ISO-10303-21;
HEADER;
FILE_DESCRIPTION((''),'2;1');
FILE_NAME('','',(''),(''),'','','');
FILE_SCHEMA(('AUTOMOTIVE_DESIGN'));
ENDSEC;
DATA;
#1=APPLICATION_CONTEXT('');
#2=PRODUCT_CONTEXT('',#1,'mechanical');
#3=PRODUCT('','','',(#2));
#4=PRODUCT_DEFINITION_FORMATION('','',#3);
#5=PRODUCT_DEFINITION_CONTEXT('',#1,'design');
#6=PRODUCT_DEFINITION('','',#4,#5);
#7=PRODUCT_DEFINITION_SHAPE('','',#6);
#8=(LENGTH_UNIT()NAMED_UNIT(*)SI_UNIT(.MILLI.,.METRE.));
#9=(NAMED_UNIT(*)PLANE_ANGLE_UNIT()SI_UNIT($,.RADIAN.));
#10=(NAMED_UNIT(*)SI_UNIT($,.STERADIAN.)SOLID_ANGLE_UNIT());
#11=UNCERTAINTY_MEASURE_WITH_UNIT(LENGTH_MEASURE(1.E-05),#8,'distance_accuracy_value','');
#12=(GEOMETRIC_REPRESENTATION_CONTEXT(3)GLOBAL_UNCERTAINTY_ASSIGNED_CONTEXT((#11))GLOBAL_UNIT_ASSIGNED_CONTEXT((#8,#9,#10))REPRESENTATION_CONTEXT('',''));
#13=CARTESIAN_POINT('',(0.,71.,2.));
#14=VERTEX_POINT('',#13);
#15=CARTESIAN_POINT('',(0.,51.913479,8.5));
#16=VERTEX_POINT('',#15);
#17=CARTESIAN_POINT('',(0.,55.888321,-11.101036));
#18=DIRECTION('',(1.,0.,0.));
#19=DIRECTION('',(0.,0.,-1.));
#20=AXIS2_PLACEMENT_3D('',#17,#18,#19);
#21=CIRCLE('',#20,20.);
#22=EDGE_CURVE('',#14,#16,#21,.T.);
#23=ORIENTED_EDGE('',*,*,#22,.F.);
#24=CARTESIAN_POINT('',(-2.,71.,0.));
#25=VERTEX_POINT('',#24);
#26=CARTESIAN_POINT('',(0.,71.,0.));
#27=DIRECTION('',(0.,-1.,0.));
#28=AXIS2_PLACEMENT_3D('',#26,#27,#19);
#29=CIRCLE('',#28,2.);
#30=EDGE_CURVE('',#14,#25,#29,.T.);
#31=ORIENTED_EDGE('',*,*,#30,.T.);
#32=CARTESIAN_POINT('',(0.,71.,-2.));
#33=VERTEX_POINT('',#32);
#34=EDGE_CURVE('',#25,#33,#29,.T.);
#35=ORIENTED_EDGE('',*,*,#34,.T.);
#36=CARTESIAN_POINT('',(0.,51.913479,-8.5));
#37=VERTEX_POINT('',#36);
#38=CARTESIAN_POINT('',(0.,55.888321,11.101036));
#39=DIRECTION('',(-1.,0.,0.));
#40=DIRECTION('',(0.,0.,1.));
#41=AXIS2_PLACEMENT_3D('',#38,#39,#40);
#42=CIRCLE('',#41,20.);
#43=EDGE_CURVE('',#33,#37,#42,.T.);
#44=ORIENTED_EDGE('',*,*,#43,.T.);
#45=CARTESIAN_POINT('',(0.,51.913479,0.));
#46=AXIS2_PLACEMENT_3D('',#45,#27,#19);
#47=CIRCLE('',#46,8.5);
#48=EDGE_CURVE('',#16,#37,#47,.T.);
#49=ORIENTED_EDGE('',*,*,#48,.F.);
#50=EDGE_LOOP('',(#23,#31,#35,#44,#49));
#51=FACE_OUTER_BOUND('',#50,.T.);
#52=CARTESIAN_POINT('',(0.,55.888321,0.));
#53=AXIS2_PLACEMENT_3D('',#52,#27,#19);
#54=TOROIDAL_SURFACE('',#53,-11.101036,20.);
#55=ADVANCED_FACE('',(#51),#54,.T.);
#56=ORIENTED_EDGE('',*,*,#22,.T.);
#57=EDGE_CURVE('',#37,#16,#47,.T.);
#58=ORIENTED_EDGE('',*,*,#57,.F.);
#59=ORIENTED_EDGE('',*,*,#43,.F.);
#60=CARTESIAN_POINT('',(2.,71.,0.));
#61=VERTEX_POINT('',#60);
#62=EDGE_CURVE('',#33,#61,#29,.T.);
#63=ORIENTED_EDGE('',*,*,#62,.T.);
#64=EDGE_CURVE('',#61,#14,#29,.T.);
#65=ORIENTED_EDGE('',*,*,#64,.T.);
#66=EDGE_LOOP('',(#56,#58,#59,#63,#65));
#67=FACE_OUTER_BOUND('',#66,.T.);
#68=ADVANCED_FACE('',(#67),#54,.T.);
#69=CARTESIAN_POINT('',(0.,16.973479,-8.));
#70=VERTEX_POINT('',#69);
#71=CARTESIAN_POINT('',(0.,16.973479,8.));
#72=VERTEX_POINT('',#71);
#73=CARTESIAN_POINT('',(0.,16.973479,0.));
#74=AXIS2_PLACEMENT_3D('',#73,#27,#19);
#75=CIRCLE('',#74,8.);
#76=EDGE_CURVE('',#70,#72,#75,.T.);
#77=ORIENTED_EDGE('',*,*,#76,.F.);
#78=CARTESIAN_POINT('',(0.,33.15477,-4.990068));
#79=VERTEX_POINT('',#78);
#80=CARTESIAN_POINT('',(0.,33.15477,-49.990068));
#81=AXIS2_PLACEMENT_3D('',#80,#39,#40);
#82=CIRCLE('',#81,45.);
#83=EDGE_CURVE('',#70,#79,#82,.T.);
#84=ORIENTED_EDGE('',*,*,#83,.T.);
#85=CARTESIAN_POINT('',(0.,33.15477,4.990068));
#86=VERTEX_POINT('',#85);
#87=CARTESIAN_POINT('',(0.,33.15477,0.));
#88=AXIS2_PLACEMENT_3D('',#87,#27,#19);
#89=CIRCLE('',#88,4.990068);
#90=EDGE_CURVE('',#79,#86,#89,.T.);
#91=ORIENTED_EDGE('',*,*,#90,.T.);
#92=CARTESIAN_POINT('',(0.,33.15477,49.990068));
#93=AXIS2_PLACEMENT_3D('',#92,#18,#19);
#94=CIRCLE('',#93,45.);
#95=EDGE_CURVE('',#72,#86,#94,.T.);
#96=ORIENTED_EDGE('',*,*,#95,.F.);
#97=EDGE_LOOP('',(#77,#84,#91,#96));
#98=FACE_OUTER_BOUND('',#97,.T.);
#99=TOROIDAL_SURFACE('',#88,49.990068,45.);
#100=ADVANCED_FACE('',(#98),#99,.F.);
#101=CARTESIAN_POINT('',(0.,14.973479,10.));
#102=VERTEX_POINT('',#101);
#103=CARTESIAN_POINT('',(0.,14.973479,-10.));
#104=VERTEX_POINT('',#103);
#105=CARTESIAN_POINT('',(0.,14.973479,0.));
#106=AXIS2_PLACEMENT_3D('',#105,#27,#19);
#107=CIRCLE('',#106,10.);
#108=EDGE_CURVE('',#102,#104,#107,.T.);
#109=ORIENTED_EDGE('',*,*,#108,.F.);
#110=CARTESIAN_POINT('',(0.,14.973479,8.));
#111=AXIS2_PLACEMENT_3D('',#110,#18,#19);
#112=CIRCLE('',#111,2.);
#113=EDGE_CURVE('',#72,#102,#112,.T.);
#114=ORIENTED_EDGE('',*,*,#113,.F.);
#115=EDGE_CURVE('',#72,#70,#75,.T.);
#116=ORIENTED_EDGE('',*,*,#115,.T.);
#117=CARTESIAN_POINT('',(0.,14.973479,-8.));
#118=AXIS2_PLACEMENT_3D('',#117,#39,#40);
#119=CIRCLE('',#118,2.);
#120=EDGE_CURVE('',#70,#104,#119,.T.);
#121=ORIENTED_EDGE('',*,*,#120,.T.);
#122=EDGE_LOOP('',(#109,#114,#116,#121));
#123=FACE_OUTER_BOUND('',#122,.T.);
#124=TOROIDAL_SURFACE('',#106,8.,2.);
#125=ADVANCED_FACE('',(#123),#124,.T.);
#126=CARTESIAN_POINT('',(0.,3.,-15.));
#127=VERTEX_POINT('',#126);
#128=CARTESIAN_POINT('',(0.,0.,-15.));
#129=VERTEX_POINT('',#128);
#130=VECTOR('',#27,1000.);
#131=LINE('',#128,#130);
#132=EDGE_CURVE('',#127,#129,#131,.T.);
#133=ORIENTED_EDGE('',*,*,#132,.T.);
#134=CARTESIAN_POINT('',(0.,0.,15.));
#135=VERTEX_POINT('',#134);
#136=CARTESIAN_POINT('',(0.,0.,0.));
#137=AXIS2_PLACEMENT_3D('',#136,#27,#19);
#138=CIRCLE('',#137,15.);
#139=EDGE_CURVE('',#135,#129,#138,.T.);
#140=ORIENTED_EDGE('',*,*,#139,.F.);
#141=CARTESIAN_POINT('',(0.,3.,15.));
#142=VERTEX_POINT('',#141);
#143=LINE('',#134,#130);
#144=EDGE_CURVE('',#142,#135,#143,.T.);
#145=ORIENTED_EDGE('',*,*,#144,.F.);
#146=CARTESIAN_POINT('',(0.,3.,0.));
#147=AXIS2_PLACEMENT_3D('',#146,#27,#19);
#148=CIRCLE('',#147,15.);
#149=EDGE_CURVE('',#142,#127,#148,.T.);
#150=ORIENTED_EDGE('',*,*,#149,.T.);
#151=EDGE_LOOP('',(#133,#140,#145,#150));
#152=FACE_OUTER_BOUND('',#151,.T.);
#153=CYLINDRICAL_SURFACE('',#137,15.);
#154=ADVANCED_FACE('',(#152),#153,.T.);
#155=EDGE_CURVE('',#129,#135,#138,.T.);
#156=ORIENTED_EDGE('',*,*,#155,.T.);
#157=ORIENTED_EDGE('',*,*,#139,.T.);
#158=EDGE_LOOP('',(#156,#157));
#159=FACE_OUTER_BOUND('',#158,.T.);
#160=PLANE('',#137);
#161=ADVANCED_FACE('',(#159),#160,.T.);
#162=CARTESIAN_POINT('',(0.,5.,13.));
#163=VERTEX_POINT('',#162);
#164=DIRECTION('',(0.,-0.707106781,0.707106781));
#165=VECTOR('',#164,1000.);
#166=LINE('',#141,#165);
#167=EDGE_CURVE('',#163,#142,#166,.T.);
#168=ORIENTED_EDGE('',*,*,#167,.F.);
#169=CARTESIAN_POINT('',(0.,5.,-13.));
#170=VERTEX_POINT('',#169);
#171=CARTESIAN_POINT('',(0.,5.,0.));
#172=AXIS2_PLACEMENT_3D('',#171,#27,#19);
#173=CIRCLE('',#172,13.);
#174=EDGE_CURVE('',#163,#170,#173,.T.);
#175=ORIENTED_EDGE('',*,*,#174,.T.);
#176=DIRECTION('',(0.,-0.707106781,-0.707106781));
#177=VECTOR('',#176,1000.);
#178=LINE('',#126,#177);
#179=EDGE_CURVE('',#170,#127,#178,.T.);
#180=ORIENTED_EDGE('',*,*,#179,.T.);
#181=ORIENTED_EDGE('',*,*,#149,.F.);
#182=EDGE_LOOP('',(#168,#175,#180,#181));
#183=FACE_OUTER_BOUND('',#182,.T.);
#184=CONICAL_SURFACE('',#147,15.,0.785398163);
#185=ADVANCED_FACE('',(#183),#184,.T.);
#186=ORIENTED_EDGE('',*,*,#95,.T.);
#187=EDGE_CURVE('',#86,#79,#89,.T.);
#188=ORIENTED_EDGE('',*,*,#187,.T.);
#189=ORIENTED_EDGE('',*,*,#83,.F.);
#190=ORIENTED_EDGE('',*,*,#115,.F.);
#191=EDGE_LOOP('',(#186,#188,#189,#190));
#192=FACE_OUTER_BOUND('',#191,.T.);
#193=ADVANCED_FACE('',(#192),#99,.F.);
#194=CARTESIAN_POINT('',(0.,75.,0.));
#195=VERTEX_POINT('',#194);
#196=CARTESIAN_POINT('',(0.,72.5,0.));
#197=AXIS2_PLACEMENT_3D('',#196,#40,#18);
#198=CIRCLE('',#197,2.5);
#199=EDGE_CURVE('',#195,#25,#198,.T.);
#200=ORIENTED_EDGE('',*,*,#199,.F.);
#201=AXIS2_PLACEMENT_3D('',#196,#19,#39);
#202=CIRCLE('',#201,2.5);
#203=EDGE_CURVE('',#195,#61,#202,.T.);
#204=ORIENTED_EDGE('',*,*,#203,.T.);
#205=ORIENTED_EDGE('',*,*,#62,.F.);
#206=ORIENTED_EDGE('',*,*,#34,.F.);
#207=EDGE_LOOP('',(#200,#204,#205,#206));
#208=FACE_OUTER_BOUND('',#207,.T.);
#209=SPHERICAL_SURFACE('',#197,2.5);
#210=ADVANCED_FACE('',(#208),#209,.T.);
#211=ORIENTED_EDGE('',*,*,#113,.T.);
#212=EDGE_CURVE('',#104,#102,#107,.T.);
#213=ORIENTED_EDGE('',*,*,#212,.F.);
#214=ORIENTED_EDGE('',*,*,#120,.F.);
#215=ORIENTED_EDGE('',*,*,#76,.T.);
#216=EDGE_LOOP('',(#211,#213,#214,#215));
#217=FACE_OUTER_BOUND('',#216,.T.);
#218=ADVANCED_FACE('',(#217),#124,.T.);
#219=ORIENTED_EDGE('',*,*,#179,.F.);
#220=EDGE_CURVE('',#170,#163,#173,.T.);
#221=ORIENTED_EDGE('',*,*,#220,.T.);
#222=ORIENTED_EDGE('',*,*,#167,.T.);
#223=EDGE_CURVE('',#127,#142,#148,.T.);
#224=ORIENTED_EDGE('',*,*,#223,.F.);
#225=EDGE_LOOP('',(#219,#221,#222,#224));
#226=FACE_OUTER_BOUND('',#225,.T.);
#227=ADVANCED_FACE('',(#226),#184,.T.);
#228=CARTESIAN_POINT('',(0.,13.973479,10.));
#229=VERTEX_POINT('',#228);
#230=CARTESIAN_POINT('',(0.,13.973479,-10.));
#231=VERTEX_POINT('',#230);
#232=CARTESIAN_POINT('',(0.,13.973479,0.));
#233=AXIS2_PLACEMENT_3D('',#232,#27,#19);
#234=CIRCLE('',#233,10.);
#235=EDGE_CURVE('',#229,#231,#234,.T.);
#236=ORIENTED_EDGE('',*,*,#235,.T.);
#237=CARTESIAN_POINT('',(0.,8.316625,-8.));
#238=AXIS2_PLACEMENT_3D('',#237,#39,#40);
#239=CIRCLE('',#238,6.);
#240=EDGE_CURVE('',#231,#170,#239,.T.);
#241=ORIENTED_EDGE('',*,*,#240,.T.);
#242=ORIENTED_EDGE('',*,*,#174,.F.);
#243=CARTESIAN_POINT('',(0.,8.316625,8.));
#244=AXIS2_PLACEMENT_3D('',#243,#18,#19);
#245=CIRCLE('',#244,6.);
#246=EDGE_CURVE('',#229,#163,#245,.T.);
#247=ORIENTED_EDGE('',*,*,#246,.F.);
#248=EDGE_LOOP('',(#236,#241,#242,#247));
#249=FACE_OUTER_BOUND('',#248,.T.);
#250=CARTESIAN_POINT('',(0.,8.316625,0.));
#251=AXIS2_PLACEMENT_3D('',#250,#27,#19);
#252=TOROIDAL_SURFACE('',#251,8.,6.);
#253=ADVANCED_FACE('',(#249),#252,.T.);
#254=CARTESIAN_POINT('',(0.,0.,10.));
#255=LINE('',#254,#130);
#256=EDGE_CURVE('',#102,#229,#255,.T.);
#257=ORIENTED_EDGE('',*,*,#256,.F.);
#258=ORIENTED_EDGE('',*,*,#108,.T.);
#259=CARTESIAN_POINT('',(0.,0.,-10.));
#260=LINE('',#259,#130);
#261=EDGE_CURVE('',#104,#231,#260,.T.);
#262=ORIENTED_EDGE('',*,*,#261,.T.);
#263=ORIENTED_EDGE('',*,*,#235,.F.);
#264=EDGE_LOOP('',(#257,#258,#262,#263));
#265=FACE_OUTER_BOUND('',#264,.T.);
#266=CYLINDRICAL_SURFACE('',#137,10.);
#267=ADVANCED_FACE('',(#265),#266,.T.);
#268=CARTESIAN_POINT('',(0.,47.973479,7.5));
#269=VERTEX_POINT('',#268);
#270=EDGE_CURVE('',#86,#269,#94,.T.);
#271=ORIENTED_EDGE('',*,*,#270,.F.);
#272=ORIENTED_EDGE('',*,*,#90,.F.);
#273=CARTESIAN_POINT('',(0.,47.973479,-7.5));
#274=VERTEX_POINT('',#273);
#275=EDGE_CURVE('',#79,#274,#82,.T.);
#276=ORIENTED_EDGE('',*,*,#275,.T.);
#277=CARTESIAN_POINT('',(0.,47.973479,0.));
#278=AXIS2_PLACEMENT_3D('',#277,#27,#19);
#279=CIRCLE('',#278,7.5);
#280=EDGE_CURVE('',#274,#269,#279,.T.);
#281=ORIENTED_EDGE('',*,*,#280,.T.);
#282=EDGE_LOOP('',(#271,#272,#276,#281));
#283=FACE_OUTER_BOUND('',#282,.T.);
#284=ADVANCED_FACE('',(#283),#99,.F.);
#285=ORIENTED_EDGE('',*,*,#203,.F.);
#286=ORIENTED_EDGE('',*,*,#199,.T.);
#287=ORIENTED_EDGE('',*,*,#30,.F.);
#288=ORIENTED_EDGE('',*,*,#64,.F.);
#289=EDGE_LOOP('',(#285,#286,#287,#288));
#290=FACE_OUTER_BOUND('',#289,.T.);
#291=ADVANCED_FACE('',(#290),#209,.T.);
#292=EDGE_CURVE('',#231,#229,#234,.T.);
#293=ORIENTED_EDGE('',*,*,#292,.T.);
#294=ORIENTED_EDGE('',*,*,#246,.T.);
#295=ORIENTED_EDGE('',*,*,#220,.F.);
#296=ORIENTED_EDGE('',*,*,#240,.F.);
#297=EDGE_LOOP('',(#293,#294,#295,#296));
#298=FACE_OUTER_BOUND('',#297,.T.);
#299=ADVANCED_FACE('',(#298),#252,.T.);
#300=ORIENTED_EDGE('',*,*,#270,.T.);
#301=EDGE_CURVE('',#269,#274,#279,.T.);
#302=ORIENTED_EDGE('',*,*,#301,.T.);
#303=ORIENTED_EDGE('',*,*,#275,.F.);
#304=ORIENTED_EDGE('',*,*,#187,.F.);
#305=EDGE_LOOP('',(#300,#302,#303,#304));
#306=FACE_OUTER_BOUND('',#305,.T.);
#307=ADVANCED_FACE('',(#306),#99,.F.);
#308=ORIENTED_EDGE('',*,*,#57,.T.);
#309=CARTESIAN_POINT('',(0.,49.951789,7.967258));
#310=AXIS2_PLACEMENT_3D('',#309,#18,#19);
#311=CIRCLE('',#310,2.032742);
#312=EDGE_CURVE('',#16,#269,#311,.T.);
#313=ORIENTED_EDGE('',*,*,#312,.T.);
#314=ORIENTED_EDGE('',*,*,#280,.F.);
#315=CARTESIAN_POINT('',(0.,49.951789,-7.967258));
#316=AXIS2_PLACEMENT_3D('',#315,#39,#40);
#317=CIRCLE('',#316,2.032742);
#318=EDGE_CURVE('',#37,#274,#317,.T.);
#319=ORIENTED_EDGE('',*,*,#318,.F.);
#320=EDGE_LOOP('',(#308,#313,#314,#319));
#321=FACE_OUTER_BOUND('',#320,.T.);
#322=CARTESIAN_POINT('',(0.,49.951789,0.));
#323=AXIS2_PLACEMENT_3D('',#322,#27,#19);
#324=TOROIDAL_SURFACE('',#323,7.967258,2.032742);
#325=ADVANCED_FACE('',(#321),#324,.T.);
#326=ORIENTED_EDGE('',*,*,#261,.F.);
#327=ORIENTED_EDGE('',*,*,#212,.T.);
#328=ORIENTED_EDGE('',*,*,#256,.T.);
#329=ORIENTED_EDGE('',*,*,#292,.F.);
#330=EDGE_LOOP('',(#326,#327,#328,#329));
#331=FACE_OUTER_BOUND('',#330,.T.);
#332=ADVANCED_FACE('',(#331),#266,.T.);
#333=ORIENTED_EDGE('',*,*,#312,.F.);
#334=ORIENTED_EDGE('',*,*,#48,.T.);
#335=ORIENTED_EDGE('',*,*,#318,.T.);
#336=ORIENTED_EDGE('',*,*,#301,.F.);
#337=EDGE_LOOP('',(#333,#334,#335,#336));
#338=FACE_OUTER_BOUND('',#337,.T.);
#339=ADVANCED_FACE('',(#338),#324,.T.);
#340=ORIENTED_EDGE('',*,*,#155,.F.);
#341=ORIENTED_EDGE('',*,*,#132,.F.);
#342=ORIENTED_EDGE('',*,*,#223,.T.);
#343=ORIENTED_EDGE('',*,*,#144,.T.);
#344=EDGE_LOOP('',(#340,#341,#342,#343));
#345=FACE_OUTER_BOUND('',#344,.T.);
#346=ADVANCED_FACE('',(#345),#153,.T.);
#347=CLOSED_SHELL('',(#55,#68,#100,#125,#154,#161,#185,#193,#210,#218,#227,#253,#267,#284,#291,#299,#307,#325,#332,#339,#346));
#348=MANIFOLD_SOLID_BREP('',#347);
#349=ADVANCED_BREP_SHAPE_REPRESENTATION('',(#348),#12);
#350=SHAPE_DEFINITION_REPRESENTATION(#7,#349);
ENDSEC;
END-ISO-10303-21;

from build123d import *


with BuildPart() as part:
    # Bishop Profile Sketch → Bishop Body Revolve (revolve)
    with BuildSketch(Plane.XY, mode=Mode.PRIVATE) as bishop_body_revolve_sk:
        with BuildLine():
            Line((0, 0), (0, 75))
            ThreePointArc((0, 75), (2.236067977, 73.618033989), (2, 71))
            ThreePointArc((2, 71), (7.831216806, 62.335784437), (8.5, 51.91347904))
            ThreePointArc((8.5, 51.91347904), (9.937529812, 49.451720204), (7.5, 47.97347904))
            ThreePointArc((7.5, 47.97347904), (4.995920105, 32.429058396), (8, 16.97347904))
            ThreePointArc((8, 16.97347904), (9.414213562, 16.387692602), (10, 14.97347904))
            Line((10, 14.97347904), (10, 13.97347904))
            ThreePointArc((10, 13.97347904), (13.69041576, 10.219036018), (13, 5))
            Line((13, 5), (15, 3))
            Line((15, 3), (15, 0))
            Line((15, 0), (0, 0))
        make_face()
    revolve(bishop_body_revolve_sk.sketch.rotate(Axis((0, 0, 0), (0, 1, 0)), 90), axis=Axis((0, 0, 0), (0, 1, 0)))


solid = part.part
